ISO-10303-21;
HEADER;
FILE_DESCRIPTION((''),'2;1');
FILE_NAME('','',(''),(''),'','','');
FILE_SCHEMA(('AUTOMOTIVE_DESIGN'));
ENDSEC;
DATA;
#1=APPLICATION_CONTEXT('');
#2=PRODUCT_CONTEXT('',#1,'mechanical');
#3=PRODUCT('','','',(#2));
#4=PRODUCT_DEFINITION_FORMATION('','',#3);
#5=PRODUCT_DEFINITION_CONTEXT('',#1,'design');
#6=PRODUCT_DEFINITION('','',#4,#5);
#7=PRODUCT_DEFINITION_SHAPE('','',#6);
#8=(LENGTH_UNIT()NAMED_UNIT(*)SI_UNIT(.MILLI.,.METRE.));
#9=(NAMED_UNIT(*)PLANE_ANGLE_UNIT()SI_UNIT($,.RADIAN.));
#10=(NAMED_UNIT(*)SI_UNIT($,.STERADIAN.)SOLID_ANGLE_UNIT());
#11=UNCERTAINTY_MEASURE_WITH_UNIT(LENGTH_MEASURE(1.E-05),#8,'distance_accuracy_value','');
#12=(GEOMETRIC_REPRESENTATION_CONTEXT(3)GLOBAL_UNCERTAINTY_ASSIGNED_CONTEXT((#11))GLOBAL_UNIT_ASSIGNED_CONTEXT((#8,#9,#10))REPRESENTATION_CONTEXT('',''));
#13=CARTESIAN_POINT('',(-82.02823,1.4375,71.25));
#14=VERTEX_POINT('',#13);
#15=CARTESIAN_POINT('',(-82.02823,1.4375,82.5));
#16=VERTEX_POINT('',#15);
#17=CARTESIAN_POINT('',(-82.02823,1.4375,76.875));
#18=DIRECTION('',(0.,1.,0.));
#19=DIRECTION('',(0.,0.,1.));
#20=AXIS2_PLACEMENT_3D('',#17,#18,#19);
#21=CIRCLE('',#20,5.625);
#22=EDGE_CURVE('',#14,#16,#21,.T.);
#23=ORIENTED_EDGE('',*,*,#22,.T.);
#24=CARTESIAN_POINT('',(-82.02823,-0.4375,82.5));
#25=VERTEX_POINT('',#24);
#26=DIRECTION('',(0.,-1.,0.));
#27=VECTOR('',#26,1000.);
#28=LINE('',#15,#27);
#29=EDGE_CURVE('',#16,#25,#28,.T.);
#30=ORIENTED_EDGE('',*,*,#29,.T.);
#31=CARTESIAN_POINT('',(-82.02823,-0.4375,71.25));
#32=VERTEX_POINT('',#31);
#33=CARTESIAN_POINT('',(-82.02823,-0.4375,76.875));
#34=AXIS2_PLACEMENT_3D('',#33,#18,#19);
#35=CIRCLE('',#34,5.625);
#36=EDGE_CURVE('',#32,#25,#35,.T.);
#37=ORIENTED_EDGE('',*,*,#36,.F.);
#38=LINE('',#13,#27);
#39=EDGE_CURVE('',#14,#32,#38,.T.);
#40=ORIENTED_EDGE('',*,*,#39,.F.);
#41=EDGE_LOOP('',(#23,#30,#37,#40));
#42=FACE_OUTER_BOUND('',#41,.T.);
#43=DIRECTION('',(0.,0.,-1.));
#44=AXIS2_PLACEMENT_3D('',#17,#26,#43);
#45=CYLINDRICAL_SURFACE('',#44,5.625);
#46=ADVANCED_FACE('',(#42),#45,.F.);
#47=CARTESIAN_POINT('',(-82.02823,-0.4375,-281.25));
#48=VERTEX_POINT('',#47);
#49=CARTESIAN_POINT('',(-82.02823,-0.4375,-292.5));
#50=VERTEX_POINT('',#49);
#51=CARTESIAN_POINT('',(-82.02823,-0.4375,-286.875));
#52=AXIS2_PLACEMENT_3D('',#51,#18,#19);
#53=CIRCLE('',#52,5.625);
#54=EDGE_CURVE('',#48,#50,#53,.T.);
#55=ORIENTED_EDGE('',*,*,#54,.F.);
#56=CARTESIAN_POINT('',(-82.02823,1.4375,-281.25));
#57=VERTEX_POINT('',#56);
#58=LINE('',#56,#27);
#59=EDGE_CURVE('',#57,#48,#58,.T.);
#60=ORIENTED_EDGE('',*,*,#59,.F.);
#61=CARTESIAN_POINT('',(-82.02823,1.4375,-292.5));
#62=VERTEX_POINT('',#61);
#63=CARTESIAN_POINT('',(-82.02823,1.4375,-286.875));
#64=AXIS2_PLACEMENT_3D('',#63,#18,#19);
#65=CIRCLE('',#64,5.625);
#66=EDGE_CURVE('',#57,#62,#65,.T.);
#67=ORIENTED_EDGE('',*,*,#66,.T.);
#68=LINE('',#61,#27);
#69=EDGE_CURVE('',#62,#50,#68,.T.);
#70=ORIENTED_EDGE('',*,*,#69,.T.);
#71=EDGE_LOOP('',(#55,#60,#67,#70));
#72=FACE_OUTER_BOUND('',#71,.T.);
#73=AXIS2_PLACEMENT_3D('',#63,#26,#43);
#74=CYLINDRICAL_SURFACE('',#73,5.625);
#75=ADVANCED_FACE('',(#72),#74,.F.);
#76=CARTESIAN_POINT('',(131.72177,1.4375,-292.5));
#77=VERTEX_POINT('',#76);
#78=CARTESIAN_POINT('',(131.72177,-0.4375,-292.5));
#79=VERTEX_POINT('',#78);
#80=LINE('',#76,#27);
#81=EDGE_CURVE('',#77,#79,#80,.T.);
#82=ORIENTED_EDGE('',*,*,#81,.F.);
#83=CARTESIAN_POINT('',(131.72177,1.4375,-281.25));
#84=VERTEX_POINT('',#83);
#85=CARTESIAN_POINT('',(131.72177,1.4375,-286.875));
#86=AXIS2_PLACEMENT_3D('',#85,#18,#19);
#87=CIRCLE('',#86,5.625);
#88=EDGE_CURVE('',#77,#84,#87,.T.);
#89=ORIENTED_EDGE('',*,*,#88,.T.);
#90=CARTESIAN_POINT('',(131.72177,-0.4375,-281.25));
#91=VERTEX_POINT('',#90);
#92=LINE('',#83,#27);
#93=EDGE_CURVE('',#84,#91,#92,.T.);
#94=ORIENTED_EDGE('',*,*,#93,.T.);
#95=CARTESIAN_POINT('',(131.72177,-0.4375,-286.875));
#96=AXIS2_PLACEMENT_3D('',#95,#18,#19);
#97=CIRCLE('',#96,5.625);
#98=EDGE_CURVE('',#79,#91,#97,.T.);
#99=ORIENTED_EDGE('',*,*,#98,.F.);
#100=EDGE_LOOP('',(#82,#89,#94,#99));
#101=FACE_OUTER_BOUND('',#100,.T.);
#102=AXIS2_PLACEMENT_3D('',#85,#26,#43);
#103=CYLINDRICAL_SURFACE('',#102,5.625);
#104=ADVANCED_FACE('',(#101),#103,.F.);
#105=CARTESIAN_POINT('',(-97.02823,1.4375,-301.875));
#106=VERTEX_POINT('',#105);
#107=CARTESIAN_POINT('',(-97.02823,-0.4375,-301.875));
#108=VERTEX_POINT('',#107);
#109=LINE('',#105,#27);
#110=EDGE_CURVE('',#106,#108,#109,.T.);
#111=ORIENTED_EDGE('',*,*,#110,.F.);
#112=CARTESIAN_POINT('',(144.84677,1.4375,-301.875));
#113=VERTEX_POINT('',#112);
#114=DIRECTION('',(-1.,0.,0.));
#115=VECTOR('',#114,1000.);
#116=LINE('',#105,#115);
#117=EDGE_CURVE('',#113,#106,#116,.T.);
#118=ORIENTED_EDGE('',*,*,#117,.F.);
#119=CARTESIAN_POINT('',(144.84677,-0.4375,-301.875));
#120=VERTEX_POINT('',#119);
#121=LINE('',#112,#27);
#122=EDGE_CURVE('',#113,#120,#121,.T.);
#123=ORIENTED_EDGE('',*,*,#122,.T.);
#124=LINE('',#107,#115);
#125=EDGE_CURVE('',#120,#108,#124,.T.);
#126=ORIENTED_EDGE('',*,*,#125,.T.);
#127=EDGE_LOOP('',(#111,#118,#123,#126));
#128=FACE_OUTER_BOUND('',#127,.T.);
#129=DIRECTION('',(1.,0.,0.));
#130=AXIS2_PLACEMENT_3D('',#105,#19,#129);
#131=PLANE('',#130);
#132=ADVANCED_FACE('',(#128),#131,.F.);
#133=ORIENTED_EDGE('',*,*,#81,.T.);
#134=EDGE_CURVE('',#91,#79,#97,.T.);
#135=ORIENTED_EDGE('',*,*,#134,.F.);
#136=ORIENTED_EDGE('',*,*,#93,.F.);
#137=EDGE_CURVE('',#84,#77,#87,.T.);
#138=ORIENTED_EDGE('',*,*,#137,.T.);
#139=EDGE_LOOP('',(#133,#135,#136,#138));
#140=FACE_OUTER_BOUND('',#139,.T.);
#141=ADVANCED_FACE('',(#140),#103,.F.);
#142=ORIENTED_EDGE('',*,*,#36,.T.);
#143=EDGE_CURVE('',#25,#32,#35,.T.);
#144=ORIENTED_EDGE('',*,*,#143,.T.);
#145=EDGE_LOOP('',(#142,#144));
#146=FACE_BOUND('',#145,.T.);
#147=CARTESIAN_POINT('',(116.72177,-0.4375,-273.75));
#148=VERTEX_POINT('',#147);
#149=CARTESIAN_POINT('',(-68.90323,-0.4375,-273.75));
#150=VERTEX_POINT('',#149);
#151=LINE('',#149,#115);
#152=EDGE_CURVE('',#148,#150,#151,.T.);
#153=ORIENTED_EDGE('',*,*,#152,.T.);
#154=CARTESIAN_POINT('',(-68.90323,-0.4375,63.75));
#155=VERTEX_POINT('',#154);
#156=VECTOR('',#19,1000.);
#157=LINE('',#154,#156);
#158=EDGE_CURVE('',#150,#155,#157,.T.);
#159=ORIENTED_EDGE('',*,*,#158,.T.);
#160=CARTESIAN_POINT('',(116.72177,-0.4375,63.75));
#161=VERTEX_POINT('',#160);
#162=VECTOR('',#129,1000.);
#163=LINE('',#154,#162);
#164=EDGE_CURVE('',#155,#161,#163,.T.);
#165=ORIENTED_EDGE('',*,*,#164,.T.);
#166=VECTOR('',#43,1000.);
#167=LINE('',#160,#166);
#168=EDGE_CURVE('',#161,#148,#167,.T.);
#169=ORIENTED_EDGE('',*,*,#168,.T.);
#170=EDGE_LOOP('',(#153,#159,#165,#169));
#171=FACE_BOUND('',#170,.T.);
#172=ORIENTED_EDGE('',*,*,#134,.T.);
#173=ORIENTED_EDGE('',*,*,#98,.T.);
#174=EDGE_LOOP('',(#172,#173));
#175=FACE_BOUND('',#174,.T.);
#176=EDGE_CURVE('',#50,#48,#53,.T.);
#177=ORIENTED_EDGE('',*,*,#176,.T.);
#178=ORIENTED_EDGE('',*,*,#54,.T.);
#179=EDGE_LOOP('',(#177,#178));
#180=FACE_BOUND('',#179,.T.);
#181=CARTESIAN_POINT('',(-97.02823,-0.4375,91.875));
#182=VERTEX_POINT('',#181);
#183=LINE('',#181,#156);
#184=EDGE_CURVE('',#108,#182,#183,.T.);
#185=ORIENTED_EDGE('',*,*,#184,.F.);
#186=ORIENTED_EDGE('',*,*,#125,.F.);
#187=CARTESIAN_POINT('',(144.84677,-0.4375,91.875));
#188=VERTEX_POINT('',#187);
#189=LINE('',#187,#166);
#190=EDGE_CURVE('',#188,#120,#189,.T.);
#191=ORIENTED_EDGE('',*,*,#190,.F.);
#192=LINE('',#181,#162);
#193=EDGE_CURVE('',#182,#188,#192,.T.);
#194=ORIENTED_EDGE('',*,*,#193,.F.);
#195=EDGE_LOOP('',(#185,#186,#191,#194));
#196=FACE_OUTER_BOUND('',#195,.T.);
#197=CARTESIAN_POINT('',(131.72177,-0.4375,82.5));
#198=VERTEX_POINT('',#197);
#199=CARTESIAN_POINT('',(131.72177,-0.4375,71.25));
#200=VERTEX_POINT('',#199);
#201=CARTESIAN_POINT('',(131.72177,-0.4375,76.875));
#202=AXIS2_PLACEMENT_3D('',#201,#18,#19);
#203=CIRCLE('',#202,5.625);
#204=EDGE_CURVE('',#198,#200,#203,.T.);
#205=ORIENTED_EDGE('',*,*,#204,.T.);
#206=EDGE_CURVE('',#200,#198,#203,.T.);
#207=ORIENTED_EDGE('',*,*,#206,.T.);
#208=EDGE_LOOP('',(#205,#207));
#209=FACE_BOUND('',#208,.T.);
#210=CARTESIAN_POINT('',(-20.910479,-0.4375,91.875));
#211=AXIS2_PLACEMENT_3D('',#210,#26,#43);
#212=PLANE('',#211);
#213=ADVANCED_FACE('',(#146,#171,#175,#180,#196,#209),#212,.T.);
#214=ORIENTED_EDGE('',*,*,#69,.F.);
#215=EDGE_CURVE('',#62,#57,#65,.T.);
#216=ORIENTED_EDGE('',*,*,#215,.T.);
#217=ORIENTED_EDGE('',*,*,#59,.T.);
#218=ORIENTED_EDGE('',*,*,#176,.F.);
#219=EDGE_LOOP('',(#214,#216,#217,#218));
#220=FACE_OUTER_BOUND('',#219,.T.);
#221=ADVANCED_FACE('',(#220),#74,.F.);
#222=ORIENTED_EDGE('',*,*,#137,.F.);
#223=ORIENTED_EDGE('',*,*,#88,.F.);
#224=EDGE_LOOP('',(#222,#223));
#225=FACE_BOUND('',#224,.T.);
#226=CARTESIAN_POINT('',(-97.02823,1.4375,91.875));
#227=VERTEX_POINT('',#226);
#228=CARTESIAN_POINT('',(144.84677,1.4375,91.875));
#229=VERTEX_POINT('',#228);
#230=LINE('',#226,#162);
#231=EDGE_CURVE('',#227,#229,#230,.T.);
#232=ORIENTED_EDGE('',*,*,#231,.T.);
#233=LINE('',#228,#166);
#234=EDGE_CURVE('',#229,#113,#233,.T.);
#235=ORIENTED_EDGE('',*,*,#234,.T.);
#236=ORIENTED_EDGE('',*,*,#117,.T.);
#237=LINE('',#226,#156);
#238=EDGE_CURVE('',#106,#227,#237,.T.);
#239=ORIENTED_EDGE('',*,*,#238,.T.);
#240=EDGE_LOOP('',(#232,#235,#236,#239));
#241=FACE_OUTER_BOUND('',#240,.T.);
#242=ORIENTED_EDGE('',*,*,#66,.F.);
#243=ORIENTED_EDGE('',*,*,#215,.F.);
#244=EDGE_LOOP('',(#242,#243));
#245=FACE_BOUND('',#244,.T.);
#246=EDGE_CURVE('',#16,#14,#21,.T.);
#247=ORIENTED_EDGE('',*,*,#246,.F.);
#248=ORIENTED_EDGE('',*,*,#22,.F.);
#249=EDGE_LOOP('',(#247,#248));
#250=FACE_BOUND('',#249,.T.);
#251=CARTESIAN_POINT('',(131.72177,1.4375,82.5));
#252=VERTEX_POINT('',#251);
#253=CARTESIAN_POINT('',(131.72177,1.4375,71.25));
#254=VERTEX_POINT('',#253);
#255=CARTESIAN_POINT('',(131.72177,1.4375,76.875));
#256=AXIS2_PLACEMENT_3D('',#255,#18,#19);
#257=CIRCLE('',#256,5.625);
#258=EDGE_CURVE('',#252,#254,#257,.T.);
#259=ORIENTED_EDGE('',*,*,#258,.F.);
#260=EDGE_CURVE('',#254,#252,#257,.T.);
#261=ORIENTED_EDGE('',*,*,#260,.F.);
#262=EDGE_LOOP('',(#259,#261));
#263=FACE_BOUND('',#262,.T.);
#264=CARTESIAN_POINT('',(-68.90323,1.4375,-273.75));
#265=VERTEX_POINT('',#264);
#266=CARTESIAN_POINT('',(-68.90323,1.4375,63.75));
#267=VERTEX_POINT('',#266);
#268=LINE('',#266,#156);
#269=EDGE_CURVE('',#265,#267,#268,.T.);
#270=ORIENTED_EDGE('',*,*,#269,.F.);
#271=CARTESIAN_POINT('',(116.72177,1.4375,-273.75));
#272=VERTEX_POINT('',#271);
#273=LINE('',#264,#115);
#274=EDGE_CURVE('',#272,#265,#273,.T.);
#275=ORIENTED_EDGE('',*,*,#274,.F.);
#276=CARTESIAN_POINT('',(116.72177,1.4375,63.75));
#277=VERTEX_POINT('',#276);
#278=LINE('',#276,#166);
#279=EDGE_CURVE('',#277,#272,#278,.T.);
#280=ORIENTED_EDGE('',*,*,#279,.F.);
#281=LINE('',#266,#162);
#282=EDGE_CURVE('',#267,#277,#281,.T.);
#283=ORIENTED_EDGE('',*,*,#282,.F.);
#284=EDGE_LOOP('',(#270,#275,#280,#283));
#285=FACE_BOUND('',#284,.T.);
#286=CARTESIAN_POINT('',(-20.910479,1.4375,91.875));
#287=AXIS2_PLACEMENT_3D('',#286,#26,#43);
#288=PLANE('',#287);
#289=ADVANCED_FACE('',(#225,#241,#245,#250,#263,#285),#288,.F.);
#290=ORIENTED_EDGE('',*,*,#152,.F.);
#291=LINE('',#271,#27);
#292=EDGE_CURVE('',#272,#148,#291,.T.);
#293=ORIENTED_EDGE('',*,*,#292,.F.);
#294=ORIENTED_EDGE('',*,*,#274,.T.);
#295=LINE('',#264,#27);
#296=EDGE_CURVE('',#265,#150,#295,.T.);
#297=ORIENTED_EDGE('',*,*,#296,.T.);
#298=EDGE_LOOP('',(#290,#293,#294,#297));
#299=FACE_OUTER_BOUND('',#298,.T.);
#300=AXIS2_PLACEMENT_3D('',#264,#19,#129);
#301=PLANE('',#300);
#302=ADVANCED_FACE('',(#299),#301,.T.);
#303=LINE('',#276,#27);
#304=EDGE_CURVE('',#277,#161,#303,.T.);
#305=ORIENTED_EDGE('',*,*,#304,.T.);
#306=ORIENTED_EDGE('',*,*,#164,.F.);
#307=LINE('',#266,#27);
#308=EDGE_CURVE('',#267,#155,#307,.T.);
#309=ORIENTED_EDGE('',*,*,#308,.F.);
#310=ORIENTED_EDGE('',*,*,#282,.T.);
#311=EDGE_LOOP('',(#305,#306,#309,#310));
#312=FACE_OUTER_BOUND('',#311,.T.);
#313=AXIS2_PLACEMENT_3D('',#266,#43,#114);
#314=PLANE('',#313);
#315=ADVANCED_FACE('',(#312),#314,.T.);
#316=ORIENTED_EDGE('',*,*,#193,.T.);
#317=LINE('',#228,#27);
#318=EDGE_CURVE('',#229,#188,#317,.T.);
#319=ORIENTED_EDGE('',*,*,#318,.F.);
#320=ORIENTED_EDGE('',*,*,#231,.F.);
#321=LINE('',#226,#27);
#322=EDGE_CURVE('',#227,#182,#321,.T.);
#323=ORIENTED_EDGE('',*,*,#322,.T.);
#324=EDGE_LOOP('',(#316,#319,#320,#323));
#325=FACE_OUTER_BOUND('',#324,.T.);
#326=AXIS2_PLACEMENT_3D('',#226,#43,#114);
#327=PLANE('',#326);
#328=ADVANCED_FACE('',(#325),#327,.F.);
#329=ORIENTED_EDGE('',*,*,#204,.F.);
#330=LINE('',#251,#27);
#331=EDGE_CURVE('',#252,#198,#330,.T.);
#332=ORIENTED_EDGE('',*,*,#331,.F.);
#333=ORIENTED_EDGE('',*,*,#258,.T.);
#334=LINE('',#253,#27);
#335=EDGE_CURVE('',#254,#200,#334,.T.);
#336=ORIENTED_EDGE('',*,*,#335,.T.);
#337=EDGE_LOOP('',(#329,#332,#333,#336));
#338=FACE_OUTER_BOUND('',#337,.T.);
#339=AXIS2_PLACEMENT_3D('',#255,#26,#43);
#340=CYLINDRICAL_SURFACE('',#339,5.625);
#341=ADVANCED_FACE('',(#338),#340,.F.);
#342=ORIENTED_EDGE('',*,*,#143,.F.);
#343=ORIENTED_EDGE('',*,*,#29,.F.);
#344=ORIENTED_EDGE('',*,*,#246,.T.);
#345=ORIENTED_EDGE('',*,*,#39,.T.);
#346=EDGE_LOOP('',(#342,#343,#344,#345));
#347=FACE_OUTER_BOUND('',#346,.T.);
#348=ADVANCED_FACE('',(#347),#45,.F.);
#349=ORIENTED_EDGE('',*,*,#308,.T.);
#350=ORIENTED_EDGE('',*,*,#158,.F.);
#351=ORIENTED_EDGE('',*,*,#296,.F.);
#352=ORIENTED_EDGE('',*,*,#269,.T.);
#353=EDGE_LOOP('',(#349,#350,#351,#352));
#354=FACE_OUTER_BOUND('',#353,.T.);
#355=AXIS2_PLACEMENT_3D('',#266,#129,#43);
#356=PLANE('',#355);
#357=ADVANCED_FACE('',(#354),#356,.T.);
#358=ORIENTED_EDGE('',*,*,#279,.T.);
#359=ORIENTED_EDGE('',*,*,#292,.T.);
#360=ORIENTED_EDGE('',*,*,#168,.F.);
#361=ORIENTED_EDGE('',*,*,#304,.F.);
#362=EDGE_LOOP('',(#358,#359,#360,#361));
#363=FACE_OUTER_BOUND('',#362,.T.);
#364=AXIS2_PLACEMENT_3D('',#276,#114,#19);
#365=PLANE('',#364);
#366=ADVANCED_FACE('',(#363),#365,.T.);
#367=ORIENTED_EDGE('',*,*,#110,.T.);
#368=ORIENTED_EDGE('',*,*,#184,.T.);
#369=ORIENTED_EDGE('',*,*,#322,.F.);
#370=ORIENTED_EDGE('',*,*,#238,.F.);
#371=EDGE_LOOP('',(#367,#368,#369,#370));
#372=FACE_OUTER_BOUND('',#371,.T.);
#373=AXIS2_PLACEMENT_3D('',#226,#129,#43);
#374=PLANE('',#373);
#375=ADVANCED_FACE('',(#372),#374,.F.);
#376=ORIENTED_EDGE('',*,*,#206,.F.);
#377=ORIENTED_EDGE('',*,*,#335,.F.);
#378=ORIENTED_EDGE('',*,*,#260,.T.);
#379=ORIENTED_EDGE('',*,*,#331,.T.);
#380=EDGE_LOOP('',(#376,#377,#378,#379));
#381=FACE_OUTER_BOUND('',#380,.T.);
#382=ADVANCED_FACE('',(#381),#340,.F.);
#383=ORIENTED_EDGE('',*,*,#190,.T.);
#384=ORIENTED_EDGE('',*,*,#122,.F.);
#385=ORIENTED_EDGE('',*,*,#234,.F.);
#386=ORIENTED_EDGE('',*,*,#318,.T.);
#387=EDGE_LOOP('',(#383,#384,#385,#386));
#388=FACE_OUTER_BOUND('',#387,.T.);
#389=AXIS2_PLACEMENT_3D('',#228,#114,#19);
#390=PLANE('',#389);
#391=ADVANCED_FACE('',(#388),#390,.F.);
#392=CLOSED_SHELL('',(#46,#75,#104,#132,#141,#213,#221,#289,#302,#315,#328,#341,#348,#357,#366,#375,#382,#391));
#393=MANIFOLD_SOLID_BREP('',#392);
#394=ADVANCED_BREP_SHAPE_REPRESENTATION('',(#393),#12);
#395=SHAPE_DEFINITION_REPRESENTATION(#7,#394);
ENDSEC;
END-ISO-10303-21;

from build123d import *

# Parameters (mm, degrees)
SKETCH1_W           = 129
SKETCH1_H           = 210
SKETCH1_R           = 3
SKETCH1_W_2         = 99
SKETCH1_H_2         = 180
BOSS_EXTRUDE1_DEPTH = 1
SCALE_1_SCALE       = 1.875


with BuildPart() as part:
    # Sketch1 → Boss-Extrude1 (new body)
    with BuildSketch(Plane(origin=(0, 0, 0), x_dir=(1, 0, 0), z_dir=(0, 1, 0))):
        with Locations((23.903865936, 105)):
            Rectangle(SKETCH1_W, SKETCH1_H)
        with Locations(Location((-32.596134064, 8, 0), (0, 0, 270))):
            Circle(SKETCH1_R, mode=Mode.SUBTRACT)
        with Locations(Location((81.403865936, 8, 0), (0, 0, 270))):
            Circle(SKETCH1_R, mode=Mode.SUBTRACT)
        with Locations(Location((81.403865936, 202, 0), (0, 0, 270))):
            Circle(SKETCH1_R, mode=Mode.SUBTRACT)
        with Locations(Location((-32.596134064, 202, 0), (0, 0, 270))):
            Circle(SKETCH1_R, mode=Mode.SUBTRACT)
        with Locations((23.903865936, 105)):
            Rectangle(SKETCH1_W_2, SKETCH1_H_2, mode=Mode.SUBTRACT)
    extrude(amount=BOSS_EXTRUDE1_DEPTH)


with BuildPart() as part_1:
    # Scale 1: scaled about (23.897690412, 0.5, -105)
    add(part.part.scale(SCALE_1_SCALE).moved(Location((-20.91047911, -0.4375, 91.875))))


solid = part_1.part
